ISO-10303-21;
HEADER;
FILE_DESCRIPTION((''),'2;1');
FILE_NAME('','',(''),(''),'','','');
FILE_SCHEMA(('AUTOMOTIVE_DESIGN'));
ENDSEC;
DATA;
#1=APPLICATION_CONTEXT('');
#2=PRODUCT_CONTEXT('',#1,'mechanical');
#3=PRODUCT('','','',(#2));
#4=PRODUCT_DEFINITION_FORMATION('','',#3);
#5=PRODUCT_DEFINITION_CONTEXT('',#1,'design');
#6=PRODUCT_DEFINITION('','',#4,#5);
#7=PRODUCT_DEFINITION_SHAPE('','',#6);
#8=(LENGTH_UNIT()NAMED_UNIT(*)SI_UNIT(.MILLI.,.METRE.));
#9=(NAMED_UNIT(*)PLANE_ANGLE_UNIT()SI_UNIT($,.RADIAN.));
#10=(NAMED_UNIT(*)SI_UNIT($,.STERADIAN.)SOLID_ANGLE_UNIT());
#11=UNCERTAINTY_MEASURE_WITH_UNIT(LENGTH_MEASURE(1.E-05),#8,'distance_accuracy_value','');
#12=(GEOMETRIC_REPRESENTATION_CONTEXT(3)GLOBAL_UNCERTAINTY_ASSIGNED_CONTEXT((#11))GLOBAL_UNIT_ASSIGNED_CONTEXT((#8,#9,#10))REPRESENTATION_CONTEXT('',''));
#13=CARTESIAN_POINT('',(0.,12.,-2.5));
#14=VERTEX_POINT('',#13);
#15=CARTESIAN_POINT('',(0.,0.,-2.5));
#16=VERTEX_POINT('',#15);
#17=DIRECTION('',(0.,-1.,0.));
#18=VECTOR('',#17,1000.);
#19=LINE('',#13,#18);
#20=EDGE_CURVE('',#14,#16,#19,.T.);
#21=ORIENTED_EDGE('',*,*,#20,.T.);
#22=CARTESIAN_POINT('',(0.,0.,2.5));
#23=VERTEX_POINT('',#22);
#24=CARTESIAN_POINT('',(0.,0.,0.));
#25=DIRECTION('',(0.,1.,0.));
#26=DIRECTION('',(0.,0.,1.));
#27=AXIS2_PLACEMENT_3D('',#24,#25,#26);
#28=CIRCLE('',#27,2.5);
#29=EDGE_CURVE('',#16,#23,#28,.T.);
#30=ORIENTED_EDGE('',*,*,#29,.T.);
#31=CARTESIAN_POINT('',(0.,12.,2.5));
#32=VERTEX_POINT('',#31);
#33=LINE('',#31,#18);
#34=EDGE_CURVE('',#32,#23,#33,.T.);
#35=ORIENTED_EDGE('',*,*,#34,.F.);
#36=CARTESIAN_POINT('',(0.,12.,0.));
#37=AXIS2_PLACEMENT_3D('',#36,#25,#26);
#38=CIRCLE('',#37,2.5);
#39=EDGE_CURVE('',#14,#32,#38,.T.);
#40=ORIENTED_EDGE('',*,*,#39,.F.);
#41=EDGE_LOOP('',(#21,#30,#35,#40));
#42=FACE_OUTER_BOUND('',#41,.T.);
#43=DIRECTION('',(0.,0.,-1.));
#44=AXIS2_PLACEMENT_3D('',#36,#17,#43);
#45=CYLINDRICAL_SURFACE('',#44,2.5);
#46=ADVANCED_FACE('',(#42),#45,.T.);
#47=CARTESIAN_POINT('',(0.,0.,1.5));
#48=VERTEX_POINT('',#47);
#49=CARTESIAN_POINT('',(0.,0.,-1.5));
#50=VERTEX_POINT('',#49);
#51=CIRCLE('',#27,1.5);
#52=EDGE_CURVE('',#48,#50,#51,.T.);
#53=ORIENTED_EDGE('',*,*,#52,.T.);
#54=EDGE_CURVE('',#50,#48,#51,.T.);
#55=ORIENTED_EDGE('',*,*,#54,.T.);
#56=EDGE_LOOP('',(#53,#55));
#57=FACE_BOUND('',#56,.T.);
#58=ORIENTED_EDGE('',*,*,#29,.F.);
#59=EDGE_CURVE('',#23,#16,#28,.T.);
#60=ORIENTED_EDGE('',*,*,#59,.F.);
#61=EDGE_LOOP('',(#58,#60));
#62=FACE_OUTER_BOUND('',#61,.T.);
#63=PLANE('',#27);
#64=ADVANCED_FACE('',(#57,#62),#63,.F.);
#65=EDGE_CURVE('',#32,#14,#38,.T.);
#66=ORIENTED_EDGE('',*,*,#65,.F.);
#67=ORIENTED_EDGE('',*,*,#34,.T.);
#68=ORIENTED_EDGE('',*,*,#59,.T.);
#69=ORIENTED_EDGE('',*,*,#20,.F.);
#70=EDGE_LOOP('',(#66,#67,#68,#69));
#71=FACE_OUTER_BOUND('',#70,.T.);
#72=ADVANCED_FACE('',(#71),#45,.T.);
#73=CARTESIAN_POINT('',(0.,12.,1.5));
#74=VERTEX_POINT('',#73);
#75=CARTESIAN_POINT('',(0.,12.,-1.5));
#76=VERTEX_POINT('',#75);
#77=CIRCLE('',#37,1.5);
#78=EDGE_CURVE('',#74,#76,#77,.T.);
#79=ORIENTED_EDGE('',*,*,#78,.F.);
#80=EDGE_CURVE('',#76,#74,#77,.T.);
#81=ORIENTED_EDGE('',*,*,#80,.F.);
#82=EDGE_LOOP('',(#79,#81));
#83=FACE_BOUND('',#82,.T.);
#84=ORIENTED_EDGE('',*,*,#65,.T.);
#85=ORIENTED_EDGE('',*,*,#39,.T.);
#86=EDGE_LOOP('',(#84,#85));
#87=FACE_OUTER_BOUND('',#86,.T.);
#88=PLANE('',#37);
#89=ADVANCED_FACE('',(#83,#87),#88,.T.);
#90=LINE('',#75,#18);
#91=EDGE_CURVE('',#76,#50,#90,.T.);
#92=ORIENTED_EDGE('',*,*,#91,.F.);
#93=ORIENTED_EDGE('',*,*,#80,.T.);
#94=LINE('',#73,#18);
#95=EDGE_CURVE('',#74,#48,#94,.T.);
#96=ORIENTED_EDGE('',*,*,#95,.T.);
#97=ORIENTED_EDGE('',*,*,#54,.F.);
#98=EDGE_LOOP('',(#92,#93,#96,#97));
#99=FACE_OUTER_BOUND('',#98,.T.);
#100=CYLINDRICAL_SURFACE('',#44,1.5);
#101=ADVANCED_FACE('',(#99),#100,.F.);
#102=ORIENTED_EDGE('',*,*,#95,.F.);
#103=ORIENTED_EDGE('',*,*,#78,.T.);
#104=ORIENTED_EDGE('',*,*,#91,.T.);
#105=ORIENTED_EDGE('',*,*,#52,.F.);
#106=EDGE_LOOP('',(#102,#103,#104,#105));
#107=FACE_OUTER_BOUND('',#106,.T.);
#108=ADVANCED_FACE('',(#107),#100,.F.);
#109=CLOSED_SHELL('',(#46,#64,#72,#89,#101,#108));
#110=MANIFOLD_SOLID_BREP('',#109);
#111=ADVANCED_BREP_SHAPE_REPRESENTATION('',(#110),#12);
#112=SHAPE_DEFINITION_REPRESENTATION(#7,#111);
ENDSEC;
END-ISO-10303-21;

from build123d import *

# Parameters (mm, degrees)
SKETCH_1_R      = 2.5
SKETCH_1_R_2    = 1.5
EXTRUDE_1_DEPTH = 12


with BuildPart() as part:
    # 草图1 → 凸台-拉伸1 (new body)
    with BuildSketch(Plane(origin=(0, 0, 0), x_dir=(1, 0, 0), z_dir=(0, 1, 0))):
        with Locations(Location((0, 0, 0), (0, 0, 270))):
            Circle(SKETCH_1_R)
        with Locations(Location((0, 0, 0), (0, 0, 270))):
            Circle(SKETCH_1_R_2, mode=Mode.SUBTRACT)
    extrude(amount=EXTRUDE_1_DEPTH)


solid = part.part
